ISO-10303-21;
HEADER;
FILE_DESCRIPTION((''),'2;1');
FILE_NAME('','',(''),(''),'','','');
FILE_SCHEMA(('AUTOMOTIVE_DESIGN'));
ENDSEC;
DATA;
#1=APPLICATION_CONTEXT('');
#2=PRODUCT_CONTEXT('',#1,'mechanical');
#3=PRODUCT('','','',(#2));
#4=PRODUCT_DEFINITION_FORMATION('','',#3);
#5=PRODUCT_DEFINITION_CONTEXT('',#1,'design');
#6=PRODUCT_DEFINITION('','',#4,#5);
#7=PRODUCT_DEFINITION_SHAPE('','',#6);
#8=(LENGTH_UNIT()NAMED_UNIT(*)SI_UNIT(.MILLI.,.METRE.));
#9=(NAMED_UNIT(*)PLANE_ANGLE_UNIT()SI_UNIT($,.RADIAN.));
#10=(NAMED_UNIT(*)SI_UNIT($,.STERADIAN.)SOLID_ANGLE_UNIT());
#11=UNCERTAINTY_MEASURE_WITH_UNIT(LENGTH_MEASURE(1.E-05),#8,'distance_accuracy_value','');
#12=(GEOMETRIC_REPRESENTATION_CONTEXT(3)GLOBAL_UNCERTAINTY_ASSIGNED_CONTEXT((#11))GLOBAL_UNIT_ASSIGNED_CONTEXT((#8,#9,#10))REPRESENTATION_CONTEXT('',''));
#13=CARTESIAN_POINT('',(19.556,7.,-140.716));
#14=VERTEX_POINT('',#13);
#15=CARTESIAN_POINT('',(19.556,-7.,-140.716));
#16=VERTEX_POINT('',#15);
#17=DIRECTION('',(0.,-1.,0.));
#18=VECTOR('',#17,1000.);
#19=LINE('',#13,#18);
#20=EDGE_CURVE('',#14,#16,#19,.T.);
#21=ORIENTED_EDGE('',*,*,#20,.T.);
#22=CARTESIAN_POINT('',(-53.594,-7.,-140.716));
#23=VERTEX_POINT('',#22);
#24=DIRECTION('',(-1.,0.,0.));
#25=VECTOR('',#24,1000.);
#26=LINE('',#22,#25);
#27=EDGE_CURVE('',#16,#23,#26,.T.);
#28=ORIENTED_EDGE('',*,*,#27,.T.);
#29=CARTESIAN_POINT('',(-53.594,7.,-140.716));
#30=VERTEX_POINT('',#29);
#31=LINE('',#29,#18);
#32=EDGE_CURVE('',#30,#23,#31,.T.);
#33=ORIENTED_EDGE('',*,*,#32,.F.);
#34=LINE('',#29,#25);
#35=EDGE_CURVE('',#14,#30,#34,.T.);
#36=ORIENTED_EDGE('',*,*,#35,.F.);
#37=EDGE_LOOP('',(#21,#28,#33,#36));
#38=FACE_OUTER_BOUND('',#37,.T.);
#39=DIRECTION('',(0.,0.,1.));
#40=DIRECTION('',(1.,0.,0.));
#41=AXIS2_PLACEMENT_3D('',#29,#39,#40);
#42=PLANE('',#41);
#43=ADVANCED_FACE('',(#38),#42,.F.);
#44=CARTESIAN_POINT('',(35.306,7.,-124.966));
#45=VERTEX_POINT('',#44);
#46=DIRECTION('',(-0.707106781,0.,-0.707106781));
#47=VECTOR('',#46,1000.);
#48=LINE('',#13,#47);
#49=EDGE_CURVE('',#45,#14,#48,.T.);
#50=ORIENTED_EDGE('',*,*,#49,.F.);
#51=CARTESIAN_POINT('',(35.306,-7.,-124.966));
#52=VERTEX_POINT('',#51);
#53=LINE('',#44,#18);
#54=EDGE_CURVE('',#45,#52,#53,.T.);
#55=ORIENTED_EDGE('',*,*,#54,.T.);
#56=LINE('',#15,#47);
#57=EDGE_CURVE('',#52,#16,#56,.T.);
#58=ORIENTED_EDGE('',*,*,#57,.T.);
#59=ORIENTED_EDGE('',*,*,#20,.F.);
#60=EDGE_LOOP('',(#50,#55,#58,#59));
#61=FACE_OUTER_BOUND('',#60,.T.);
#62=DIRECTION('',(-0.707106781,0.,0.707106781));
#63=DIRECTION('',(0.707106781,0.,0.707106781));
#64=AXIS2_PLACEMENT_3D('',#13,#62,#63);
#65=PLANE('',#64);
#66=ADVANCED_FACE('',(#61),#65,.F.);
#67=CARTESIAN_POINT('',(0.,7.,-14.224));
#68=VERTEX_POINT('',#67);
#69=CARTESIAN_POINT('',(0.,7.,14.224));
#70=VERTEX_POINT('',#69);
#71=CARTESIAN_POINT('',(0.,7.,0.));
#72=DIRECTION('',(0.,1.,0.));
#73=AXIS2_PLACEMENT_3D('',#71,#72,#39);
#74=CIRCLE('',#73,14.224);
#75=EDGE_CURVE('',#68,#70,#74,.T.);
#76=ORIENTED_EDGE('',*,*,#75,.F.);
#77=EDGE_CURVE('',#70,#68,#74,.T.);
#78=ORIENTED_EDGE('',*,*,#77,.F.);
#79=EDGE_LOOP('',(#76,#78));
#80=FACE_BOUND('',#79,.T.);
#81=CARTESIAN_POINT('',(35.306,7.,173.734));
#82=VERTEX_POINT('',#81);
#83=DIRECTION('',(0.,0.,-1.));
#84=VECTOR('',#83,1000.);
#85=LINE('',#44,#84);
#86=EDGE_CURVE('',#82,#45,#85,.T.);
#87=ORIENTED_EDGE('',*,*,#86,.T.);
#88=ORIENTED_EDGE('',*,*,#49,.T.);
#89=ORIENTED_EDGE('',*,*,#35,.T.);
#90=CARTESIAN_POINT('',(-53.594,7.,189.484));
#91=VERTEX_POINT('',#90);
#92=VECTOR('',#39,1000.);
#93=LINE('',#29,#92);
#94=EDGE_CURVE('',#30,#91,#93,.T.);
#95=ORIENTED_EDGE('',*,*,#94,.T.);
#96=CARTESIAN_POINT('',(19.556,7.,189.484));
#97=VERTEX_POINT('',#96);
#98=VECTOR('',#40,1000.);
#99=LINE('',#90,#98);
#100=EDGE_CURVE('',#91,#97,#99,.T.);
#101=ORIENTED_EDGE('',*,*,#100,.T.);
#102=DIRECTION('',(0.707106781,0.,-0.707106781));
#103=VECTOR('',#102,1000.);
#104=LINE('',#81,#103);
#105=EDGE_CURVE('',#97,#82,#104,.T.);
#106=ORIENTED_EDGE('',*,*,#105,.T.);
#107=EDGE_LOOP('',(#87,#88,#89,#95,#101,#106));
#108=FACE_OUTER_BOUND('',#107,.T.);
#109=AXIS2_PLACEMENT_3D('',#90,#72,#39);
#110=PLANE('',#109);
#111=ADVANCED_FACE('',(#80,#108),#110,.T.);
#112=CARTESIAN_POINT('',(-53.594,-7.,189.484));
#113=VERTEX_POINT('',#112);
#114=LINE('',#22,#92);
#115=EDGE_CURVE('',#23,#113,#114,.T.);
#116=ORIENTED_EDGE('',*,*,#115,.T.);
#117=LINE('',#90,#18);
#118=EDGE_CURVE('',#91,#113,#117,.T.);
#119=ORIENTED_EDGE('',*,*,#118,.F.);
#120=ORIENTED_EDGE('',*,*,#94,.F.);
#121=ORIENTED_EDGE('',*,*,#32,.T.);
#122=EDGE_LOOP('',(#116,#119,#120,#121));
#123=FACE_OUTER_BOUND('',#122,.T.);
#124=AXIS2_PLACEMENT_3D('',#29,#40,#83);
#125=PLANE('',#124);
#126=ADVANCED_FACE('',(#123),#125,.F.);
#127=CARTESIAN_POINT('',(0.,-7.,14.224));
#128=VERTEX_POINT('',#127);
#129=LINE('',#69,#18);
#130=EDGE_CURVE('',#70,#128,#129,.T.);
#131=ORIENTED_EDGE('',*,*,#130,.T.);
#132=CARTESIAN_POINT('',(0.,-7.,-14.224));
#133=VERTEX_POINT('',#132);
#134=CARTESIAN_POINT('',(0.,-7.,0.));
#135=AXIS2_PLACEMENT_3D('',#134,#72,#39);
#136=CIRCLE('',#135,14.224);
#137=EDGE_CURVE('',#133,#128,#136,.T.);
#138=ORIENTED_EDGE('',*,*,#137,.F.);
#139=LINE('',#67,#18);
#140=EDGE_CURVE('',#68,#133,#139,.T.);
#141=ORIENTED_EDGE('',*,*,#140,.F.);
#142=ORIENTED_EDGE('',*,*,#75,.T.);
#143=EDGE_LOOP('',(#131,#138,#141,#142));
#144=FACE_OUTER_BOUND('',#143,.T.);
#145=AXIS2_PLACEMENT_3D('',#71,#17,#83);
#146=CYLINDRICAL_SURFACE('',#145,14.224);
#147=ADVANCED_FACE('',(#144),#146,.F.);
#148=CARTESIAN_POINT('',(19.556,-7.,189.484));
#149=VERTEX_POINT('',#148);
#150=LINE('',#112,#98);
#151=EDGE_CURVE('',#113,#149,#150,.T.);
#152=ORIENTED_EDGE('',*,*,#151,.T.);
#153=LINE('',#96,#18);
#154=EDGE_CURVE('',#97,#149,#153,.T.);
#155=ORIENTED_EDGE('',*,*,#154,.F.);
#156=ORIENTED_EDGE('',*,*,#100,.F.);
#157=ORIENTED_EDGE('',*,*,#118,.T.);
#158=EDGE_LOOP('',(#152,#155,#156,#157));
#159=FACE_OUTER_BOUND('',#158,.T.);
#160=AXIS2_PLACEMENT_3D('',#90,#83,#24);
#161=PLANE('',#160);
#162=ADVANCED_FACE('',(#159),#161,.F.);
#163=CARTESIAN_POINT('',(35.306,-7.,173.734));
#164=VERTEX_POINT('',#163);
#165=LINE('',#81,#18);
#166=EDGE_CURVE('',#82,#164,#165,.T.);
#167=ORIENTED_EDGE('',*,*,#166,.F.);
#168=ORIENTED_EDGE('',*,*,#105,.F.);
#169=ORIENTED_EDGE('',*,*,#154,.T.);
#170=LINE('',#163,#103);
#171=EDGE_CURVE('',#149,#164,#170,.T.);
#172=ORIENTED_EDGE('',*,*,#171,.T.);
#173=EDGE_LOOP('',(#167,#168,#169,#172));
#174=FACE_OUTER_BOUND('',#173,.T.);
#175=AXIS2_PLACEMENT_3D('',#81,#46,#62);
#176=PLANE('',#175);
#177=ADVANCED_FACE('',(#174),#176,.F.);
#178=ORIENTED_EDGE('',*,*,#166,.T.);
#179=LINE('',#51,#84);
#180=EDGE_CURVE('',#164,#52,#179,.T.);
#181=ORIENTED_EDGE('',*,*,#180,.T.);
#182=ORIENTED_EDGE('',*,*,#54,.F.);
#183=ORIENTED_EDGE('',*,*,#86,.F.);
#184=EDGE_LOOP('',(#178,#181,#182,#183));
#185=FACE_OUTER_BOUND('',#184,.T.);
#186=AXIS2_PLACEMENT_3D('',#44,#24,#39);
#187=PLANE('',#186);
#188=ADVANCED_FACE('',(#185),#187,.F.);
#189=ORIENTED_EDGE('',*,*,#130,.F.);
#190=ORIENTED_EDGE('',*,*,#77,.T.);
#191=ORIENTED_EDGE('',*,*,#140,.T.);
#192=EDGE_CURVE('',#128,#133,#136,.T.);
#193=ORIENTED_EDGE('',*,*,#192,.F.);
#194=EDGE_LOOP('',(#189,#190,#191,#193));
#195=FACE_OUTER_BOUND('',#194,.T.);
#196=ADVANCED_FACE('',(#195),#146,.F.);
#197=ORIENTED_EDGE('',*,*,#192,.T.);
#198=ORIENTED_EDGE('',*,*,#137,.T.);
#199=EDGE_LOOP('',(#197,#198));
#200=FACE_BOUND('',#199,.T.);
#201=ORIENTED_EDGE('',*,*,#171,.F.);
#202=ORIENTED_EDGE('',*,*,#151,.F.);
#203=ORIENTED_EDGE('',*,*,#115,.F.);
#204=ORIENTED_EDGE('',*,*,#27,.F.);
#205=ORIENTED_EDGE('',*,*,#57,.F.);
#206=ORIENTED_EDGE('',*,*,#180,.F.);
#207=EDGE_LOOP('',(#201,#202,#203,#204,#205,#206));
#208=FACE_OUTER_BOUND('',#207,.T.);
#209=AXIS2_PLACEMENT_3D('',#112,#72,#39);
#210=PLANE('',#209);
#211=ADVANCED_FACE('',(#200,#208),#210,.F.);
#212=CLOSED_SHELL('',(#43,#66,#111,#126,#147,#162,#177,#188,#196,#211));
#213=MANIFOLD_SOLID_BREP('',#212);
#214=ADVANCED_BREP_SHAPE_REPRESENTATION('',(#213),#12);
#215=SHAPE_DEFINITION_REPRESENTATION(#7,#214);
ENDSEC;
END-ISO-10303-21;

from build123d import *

# Parameters (mm, degrees)
SKETCH3_R           = 14.224
BOSS_EXTRUDE1_DEPTH = 7


with BuildPart() as part:
    # Sketch3 → Boss-Extrude1 (new, symmetric)
    with BuildSketch(Plane(origin=(0, 0, 0), x_dir=(1, 0, 0), z_dir=(0, 1, 0))):
        Polygon((19.556, 140.716), (35.306, 124.966), (35.306, -173.734), (19.556, -189.484), (-53.594, -189.484), (-53.594, 140.716), align=None)
        with Locations(Location((0, 0, 0), (0, 0, 270))):
            Circle(SKETCH3_R, mode=Mode.SUBTRACT)
    extrude(amount=BOSS_EXTRUDE1_DEPTH, both=True)


solid = part.part
